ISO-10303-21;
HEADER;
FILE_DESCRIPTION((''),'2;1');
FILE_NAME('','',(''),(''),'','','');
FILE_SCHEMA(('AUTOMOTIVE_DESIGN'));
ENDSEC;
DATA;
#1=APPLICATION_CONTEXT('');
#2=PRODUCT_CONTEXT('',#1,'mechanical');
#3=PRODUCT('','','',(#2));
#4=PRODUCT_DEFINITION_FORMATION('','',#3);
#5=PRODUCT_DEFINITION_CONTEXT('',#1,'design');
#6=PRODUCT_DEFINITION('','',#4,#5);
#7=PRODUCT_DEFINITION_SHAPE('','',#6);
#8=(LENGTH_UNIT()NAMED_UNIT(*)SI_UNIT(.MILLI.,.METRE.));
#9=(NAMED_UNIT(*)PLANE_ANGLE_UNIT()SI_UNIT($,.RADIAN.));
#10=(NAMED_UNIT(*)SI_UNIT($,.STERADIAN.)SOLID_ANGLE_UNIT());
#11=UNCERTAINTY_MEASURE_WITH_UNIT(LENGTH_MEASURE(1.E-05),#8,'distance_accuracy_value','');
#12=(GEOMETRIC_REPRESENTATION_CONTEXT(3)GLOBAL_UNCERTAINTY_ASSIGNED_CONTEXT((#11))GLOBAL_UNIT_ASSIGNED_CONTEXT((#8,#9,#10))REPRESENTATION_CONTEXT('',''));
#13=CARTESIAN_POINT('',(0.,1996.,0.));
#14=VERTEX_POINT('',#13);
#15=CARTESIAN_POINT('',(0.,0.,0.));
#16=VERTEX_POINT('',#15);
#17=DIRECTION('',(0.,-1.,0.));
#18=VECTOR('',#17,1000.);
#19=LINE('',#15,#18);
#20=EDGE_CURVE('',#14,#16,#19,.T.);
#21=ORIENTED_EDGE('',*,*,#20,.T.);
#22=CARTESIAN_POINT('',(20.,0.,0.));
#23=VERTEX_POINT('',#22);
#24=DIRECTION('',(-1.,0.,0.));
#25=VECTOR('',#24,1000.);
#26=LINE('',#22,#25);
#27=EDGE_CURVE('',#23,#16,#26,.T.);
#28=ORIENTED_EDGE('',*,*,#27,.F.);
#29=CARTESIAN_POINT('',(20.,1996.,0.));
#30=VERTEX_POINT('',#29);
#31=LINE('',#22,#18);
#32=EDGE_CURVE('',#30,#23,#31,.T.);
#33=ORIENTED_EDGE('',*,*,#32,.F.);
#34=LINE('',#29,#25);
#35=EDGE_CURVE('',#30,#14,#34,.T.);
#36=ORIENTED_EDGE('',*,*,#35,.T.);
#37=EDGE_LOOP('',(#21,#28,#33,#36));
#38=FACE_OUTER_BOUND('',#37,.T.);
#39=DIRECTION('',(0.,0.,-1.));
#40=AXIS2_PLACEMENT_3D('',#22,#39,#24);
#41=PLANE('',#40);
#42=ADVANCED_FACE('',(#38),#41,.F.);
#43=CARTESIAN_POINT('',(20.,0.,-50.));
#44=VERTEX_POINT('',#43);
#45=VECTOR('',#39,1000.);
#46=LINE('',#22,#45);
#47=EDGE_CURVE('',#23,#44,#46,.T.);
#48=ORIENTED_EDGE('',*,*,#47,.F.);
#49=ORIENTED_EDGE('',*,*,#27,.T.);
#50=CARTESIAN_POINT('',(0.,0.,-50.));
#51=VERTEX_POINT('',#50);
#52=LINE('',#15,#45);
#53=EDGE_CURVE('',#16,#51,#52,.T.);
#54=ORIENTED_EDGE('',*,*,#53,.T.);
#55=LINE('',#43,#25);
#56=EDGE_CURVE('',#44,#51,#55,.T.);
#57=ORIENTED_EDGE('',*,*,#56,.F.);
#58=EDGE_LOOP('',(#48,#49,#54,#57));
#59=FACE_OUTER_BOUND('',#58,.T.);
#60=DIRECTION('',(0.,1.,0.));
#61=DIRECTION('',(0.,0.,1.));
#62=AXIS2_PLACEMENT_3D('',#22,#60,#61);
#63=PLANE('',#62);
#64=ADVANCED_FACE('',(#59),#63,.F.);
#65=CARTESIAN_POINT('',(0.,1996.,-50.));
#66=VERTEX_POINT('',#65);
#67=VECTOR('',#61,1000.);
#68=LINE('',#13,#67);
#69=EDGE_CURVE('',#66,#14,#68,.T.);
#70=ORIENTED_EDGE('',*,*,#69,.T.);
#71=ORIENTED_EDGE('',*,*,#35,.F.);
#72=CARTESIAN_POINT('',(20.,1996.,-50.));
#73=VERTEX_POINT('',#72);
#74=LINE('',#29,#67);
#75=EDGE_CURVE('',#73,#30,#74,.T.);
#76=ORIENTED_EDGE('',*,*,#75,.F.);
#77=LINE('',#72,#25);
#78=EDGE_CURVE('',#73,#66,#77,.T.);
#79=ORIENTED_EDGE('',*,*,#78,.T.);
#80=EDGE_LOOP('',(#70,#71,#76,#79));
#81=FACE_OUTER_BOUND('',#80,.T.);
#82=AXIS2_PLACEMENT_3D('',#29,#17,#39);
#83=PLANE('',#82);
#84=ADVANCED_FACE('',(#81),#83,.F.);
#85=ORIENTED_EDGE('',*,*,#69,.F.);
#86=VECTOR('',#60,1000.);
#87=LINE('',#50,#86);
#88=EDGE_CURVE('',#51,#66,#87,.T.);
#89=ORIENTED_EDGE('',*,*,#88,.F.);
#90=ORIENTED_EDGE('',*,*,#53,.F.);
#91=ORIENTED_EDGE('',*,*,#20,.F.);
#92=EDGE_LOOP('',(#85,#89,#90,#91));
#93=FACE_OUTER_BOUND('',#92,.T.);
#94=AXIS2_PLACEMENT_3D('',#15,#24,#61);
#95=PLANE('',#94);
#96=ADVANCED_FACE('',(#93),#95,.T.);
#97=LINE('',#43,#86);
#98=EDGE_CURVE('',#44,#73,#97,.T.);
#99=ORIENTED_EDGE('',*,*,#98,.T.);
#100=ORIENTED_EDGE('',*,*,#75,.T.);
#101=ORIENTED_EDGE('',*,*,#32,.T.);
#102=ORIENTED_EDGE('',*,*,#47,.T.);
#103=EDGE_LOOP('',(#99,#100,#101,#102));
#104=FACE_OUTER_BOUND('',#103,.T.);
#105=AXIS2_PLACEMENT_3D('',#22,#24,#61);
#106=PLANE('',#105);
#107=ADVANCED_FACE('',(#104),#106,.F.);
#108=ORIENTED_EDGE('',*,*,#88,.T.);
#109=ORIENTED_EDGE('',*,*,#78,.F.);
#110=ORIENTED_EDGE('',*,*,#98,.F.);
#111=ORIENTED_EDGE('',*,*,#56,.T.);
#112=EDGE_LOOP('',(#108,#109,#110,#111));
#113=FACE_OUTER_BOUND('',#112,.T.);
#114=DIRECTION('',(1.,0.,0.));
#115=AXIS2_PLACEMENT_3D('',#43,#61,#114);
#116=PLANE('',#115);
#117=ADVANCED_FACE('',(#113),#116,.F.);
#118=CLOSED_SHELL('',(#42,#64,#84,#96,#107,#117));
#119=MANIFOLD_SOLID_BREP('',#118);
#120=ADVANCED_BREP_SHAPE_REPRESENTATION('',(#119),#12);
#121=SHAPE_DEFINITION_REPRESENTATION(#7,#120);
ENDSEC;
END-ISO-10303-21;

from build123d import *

# Parameters (mm, degrees)
SKETCH1_W           = 50
SKETCH1_H           = 1996
BOSS_EXTRUDE1_DEPTH = 20


with BuildPart() as part:
    # Sketch1 → Boss-Extrude1 (new body)
    with BuildSketch(Plane(origin=(0, 0, 0), x_dir=(0, 0, -1), z_dir=(1, 0, 0))):
        with Locations((25, 998)):
            Rectangle(SKETCH1_W, SKETCH1_H)
    extrude(amount=BOSS_EXTRUDE1_DEPTH)


solid = part.part
